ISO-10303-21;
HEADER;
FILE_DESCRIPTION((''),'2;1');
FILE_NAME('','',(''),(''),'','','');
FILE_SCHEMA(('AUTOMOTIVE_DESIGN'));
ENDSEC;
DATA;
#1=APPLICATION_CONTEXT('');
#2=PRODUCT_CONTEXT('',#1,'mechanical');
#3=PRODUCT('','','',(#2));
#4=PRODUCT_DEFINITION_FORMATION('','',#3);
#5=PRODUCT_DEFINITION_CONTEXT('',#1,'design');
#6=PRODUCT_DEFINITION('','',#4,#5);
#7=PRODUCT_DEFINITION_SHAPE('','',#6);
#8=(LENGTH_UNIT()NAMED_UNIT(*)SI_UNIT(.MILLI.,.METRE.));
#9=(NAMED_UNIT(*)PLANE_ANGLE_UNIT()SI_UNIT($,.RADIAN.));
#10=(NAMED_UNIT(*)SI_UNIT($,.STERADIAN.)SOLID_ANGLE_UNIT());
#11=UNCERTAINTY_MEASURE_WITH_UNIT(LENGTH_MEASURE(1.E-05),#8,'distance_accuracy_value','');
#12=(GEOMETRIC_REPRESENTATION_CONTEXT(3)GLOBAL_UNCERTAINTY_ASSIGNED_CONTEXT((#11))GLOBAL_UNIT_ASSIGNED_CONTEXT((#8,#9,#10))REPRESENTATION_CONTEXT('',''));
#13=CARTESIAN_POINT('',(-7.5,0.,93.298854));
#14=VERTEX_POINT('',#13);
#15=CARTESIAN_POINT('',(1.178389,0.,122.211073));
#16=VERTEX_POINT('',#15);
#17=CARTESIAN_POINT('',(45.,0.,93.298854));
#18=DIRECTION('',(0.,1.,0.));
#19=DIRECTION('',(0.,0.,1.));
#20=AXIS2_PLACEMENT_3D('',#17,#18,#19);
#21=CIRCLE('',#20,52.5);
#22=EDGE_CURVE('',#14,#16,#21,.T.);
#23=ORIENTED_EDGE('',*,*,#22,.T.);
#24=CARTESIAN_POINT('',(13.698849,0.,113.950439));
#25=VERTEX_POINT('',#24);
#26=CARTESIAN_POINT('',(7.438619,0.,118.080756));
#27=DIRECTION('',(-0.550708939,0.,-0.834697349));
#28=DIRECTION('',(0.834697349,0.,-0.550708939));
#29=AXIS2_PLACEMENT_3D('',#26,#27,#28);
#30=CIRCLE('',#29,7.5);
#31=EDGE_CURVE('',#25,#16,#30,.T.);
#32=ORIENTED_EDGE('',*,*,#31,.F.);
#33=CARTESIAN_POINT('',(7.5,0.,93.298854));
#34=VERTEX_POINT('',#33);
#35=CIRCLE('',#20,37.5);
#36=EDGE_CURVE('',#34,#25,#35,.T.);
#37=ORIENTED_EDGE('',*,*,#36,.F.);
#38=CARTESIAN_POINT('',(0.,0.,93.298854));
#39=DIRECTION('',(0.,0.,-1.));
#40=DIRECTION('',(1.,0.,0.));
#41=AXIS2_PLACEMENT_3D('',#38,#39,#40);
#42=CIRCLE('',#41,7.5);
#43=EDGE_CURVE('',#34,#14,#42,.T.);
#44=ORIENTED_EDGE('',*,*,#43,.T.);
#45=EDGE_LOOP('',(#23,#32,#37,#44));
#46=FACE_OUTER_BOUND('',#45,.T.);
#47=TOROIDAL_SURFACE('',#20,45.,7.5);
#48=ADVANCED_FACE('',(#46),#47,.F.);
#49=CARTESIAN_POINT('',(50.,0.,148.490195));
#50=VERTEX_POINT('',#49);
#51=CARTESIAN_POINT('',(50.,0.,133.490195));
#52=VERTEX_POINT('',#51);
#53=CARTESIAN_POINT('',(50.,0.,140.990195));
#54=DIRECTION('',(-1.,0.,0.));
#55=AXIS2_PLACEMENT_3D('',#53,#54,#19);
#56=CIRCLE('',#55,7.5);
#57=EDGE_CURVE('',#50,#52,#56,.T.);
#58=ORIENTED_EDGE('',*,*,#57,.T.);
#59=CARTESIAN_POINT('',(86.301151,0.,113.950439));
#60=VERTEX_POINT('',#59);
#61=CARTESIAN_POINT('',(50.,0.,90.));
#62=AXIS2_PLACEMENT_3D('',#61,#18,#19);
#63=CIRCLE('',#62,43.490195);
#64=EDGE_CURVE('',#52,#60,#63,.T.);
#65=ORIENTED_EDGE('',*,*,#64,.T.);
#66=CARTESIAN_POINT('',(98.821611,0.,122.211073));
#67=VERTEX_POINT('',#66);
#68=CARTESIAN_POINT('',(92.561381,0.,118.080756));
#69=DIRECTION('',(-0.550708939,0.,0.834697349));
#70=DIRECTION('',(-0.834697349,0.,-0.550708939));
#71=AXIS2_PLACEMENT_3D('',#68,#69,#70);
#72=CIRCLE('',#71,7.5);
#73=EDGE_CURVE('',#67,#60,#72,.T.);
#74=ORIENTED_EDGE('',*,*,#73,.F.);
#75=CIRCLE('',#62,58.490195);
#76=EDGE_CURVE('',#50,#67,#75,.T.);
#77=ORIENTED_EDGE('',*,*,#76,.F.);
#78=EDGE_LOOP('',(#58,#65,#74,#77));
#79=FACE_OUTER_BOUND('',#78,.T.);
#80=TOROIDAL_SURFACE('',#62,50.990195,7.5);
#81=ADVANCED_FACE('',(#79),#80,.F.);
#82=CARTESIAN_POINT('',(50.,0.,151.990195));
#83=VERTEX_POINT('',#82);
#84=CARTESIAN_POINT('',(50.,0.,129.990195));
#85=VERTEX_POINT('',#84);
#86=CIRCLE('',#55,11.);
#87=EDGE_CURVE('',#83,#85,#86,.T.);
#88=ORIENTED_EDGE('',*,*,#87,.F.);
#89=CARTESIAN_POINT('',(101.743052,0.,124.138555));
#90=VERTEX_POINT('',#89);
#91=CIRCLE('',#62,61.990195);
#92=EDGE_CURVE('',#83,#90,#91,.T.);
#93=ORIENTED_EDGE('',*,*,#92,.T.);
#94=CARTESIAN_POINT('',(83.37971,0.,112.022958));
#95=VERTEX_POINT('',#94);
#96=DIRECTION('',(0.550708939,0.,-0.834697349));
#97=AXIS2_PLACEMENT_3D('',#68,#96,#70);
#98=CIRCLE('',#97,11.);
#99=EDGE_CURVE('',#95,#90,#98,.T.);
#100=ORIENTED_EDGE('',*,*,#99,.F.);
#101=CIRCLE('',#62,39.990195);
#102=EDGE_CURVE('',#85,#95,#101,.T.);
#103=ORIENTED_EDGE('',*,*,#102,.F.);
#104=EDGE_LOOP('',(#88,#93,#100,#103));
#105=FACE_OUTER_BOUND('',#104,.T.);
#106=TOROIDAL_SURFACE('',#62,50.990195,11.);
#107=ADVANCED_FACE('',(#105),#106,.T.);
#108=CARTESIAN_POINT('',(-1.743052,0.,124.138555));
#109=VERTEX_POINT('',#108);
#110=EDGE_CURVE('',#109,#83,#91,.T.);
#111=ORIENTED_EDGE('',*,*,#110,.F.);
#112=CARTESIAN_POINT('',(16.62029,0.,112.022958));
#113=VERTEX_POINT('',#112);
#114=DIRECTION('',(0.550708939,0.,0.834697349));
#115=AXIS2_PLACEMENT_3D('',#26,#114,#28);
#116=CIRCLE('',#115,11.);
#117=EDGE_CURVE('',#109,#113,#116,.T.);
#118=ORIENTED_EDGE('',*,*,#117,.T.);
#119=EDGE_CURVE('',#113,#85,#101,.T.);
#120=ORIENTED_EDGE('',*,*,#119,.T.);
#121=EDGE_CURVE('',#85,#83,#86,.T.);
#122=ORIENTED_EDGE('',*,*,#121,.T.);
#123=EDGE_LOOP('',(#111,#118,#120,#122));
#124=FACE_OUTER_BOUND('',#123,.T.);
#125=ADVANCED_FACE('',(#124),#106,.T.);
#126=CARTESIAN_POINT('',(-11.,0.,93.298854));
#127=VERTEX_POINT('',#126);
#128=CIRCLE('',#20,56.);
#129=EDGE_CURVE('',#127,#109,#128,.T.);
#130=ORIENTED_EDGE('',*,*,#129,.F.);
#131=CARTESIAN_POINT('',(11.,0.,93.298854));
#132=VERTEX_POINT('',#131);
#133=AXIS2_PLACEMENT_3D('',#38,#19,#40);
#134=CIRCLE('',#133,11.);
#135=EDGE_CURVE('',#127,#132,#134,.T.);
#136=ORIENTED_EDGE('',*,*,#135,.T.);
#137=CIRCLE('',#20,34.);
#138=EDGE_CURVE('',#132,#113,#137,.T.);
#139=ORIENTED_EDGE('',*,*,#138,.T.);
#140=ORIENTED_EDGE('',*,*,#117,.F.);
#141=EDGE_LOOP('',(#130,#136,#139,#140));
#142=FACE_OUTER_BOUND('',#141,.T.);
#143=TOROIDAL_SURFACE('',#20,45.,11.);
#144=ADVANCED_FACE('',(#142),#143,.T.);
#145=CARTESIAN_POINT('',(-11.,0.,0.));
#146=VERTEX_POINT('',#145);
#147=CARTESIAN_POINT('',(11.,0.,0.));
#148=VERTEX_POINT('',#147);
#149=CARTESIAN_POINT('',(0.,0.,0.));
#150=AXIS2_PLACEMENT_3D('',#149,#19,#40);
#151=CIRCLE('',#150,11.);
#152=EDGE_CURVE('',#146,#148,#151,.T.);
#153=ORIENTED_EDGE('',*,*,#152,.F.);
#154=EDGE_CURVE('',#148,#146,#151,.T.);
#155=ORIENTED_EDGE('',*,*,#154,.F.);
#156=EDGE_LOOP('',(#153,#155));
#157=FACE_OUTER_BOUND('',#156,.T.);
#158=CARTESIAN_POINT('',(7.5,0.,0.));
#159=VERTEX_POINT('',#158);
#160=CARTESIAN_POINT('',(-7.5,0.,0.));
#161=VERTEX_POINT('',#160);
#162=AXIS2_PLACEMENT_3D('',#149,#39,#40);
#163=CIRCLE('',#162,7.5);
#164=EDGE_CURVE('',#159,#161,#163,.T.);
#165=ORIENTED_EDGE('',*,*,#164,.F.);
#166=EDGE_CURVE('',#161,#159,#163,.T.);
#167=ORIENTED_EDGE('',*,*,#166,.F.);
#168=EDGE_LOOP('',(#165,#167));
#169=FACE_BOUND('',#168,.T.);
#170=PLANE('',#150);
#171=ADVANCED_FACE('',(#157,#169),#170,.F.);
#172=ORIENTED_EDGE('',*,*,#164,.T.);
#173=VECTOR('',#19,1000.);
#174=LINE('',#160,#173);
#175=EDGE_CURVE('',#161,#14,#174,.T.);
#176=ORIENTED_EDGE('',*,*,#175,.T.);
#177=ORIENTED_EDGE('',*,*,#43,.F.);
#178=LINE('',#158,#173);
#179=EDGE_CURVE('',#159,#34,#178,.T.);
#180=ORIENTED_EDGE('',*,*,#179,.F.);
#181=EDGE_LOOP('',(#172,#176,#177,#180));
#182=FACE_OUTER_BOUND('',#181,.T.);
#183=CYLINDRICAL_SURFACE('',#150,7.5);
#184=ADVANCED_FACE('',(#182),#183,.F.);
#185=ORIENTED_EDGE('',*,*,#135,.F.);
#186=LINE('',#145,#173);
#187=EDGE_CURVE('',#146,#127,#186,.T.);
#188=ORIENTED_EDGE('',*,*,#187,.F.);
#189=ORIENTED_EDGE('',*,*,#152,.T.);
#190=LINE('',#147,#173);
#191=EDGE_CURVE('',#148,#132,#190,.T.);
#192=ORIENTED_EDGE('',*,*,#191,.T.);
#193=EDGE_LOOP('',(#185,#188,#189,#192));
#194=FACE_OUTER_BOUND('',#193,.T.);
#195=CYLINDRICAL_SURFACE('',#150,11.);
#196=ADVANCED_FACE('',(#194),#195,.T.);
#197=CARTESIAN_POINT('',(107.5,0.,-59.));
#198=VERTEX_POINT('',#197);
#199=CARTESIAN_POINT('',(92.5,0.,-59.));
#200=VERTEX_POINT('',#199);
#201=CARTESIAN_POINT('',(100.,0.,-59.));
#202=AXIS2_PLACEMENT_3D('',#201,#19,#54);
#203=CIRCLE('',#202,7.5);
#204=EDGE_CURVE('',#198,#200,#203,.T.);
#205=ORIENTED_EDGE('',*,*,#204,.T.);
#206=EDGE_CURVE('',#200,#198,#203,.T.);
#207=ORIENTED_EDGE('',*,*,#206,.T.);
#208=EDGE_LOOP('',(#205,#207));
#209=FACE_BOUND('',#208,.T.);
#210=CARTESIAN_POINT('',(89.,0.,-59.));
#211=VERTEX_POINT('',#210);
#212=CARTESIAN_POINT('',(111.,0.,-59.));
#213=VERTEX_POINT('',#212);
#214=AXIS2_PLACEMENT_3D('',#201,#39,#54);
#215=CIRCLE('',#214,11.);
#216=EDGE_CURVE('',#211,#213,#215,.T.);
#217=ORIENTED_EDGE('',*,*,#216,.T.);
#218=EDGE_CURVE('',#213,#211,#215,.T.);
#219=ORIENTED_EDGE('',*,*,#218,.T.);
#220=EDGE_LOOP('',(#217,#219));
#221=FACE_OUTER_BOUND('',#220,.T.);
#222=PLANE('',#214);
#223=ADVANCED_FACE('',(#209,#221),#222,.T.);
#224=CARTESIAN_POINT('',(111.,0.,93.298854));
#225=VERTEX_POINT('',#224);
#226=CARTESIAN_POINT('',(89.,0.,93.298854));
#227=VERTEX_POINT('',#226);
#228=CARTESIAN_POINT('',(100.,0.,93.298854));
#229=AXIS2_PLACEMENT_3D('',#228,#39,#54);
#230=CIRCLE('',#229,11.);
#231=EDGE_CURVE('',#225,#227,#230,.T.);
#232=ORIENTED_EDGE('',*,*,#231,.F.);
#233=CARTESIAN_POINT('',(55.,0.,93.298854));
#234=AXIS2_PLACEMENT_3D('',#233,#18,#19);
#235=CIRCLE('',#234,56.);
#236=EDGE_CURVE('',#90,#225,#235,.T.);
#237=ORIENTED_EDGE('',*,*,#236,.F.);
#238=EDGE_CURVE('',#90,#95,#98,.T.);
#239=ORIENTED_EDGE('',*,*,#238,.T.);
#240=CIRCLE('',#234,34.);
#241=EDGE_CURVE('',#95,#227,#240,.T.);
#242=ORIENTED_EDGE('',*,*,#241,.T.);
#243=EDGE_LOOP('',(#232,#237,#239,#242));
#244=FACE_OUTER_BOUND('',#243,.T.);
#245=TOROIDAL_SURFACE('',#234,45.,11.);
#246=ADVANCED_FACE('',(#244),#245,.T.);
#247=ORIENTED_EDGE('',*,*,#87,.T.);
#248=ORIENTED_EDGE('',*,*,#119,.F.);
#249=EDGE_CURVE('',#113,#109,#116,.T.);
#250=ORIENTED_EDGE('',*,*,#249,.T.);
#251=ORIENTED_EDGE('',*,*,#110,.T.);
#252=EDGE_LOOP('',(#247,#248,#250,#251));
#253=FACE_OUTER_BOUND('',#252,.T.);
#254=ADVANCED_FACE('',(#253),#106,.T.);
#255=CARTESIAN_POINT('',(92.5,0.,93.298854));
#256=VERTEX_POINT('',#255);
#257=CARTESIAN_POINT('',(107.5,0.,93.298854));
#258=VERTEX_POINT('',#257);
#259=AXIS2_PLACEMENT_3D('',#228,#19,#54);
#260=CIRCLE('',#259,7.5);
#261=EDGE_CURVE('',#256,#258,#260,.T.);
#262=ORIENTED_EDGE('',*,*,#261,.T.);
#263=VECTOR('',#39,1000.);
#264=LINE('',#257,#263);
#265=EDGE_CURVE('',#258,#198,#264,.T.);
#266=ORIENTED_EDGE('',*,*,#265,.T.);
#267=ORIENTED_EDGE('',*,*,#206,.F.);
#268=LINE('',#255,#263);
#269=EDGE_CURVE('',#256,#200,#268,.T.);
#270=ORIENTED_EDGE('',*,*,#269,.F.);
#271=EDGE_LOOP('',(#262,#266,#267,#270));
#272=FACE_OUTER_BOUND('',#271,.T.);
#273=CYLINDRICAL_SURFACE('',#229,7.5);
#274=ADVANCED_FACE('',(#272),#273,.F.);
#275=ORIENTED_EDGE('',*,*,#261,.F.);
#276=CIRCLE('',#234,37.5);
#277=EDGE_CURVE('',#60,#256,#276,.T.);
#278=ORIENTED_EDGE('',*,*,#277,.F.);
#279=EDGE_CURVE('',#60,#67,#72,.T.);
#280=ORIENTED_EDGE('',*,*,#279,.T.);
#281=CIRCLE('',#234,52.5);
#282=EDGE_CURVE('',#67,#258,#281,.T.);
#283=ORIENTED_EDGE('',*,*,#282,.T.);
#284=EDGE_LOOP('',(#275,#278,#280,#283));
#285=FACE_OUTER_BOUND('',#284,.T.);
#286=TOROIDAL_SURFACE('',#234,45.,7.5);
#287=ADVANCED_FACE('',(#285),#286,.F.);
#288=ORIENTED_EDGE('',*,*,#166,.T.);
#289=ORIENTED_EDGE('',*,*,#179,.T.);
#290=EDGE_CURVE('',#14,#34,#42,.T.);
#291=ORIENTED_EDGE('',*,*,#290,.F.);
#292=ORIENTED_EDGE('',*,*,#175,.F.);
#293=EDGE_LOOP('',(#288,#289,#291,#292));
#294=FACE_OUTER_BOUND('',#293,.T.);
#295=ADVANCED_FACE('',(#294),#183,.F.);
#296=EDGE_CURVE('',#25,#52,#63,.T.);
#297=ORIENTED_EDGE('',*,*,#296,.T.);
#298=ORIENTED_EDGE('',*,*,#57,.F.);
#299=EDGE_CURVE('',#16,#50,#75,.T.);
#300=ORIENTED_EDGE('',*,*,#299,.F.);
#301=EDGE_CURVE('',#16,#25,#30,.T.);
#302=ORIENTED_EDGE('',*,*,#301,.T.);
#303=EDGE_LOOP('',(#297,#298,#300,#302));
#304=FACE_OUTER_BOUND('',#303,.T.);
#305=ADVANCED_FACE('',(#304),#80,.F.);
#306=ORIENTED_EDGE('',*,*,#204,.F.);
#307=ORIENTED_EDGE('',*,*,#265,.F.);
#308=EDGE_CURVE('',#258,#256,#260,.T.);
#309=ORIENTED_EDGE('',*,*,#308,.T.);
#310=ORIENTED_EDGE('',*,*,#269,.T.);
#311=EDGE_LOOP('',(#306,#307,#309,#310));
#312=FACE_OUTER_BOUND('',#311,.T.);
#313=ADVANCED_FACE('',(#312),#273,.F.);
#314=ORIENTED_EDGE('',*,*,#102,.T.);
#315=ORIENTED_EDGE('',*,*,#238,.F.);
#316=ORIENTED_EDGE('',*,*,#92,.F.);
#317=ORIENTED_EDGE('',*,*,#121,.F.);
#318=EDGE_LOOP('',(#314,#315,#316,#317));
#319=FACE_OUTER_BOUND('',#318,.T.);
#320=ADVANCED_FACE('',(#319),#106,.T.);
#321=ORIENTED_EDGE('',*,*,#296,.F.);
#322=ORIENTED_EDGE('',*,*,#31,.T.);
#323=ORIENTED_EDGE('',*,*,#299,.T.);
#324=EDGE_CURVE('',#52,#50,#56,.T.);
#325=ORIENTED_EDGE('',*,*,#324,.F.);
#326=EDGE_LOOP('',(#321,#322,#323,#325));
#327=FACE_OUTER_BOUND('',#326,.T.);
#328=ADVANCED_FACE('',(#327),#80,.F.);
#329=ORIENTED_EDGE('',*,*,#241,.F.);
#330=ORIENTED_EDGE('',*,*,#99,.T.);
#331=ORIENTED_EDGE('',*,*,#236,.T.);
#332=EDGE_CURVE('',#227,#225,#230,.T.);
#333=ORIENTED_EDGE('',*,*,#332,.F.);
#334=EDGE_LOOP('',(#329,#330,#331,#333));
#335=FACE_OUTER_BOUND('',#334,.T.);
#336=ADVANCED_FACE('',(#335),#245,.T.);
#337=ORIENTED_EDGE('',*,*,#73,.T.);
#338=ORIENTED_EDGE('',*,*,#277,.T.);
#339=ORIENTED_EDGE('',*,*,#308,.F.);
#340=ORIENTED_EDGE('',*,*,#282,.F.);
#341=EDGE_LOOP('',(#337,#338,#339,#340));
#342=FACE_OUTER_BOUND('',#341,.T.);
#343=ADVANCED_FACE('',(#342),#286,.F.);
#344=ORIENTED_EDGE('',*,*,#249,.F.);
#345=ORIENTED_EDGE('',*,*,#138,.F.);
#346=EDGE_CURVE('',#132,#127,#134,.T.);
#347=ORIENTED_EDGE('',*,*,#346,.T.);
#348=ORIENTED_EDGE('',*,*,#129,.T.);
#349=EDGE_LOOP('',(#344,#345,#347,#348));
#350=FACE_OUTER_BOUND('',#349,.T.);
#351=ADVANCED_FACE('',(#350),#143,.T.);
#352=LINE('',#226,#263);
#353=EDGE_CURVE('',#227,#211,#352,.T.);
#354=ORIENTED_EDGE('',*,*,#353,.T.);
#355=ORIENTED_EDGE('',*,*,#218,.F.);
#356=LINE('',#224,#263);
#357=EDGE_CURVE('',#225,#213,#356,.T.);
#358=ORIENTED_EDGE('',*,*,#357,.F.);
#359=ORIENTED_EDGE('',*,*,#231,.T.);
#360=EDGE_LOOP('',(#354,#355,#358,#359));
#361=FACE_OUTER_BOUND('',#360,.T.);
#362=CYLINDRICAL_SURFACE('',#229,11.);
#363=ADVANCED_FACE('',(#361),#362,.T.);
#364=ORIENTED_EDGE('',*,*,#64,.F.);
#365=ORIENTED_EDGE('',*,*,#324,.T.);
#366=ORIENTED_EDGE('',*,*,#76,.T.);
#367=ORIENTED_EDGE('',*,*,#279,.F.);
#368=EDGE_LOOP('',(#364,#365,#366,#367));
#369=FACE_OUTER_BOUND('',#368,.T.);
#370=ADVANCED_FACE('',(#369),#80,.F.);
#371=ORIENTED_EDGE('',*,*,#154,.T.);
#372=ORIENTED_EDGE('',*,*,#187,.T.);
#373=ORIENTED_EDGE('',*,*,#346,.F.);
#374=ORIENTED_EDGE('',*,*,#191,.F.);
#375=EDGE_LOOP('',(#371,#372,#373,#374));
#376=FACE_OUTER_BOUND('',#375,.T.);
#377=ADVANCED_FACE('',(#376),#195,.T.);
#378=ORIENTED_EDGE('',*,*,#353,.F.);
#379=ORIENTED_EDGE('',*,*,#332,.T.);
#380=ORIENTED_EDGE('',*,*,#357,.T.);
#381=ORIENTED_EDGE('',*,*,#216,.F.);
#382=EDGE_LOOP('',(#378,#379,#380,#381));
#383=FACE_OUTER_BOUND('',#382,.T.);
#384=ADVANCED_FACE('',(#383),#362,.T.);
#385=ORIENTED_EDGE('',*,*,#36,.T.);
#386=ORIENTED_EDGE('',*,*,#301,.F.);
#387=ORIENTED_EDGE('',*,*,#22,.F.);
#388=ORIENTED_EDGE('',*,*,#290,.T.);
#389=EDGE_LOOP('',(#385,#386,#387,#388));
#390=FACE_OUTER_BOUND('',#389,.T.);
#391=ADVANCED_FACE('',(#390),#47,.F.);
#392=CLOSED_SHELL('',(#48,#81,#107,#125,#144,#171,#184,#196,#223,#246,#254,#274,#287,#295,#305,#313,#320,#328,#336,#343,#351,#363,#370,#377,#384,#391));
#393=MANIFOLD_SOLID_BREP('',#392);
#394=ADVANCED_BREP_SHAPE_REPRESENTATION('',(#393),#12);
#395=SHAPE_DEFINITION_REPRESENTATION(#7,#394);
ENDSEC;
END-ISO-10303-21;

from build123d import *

# Parameters (mm, degrees)
SKETCH1_R   = 11
SKETCH1_R_2 = 7.5


with BuildPart() as part:
    # Sweep1: sweep along a path in Sketch2
    with BuildLine(Plane(origin=(0, 0, 0), x_dir=(1, 0, 0), z_dir=(0, 1, 0))) as sweep1_path:
        Line((0, 0), (0, -93.298854008))
        ThreePointArc((0, -93.298854008), (1.899755617, -106.235968606), (7.438619295, -118.080756266))
        ThreePointArc((7.438619295, -118.080756266), (50, -140.990195136), (92.561380705, -118.080756266))
        ThreePointArc((92.561380705, -118.080756266), (98.100244383, -106.235968606), (100, -93.298854008))
        Line((100, -93.298854008), (100, 59.000000002))
    # Sketch1 → Sweep1 (sweep)
    with BuildSketch(Plane.XY):
        Circle(SKETCH1_R)
        Circle(SKETCH1_R_2, mode=Mode.SUBTRACT)
    sweep(path=sweep1_path.line)


solid = part.part
